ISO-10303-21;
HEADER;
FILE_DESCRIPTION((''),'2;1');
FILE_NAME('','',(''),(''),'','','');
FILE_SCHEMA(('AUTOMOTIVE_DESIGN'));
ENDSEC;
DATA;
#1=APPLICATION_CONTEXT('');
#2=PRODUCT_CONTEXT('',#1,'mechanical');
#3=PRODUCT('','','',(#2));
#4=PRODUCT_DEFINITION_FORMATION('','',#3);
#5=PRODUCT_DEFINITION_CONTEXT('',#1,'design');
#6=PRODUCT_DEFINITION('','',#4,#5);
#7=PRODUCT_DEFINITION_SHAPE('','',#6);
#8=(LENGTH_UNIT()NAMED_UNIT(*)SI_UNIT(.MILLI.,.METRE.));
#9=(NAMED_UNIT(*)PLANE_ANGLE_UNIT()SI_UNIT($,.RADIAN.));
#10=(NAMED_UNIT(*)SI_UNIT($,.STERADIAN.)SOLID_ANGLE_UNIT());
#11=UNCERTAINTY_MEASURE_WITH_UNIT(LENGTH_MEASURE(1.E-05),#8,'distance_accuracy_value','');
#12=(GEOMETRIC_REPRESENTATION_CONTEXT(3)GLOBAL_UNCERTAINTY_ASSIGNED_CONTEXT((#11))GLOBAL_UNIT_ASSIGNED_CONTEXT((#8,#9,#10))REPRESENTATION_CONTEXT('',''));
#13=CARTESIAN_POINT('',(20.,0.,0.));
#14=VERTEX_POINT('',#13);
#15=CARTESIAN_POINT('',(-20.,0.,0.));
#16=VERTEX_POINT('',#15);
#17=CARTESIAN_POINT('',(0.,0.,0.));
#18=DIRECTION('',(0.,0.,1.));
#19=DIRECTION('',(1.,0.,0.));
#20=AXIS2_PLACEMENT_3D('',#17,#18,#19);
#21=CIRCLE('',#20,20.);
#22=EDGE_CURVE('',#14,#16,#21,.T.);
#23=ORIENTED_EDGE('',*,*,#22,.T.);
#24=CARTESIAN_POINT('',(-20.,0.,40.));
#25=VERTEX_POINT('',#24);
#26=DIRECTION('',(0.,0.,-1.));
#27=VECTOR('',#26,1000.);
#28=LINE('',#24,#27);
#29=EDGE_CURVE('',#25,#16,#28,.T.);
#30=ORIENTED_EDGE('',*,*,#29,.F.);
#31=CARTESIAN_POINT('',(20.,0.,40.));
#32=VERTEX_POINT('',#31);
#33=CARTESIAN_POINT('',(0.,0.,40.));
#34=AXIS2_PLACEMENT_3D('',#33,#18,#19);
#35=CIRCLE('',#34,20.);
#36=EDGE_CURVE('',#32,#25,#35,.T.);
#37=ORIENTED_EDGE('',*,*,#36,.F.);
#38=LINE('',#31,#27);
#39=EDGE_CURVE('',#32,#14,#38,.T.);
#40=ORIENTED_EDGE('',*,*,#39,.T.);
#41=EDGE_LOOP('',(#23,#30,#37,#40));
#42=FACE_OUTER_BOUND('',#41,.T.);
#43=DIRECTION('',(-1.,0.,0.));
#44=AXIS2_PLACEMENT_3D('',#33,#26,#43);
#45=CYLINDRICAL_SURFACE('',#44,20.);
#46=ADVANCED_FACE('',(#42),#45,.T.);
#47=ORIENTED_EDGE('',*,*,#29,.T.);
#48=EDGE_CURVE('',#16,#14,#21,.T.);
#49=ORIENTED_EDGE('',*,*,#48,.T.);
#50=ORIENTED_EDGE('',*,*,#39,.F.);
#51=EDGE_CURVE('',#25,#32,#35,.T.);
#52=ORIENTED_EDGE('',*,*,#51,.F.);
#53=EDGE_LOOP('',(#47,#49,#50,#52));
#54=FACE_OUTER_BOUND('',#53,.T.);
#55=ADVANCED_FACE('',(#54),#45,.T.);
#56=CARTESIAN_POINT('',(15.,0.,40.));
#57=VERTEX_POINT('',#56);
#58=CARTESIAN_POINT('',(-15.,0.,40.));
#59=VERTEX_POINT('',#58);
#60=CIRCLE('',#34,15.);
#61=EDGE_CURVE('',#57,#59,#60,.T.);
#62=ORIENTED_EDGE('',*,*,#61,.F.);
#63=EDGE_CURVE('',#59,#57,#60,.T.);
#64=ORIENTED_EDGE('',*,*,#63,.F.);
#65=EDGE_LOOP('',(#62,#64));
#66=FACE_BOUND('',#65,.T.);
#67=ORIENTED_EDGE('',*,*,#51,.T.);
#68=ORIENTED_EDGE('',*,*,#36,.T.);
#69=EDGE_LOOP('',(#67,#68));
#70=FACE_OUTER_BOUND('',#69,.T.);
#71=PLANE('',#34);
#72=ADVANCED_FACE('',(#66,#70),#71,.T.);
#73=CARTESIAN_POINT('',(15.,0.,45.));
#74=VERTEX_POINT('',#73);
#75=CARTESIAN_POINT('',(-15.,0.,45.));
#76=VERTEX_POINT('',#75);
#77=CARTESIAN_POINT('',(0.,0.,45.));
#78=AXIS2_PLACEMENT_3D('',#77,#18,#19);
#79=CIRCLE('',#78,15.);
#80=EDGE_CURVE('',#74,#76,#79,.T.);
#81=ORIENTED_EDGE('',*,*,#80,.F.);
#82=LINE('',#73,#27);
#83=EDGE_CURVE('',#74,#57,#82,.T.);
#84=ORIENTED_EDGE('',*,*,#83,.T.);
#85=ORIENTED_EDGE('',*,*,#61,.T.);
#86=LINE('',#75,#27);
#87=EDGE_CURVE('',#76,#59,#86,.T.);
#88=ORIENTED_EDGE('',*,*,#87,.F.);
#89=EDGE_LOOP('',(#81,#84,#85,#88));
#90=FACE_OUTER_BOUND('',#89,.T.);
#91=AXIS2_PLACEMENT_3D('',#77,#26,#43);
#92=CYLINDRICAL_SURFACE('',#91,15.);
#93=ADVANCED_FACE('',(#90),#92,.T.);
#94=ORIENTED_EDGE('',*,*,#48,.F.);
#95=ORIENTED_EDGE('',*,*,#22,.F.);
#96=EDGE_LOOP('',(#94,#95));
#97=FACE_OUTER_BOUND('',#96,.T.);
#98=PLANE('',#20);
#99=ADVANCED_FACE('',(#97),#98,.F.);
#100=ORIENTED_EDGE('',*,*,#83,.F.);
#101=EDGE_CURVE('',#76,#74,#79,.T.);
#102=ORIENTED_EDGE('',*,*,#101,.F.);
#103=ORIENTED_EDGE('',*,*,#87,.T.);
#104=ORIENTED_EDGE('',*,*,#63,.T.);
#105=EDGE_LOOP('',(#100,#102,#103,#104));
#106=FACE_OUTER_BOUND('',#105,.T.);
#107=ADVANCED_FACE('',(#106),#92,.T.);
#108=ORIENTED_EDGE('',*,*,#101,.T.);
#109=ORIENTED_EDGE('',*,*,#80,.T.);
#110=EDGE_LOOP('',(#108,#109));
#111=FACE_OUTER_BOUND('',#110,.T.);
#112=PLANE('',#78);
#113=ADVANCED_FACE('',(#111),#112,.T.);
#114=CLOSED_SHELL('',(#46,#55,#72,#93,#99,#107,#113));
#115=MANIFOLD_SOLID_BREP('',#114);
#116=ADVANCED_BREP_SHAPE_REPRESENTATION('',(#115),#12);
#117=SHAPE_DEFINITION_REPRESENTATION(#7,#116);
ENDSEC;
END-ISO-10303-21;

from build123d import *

# Parameters (mm, degrees)
SKETCH1_R           = 20
BOSS_EXTRUDE1_DEPTH = 40
SKETCH2_R           = 15
BOSS_EXTRUDE2_DEPTH = 5


with BuildPart() as part:
    # Sketch1 → Boss-Extrude1 (new body)
    with BuildSketch(Plane.XY):
        Circle(SKETCH1_R)
    extrude(amount=BOSS_EXTRUDE1_DEPTH)

    # Sketch2 → Boss-Extrude2 (add)
    with BuildSketch(Plane.XY.offset(40)):
        Circle(SKETCH2_R)
    extrude(amount=BOSS_EXTRUDE2_DEPTH)


solid = part.part
